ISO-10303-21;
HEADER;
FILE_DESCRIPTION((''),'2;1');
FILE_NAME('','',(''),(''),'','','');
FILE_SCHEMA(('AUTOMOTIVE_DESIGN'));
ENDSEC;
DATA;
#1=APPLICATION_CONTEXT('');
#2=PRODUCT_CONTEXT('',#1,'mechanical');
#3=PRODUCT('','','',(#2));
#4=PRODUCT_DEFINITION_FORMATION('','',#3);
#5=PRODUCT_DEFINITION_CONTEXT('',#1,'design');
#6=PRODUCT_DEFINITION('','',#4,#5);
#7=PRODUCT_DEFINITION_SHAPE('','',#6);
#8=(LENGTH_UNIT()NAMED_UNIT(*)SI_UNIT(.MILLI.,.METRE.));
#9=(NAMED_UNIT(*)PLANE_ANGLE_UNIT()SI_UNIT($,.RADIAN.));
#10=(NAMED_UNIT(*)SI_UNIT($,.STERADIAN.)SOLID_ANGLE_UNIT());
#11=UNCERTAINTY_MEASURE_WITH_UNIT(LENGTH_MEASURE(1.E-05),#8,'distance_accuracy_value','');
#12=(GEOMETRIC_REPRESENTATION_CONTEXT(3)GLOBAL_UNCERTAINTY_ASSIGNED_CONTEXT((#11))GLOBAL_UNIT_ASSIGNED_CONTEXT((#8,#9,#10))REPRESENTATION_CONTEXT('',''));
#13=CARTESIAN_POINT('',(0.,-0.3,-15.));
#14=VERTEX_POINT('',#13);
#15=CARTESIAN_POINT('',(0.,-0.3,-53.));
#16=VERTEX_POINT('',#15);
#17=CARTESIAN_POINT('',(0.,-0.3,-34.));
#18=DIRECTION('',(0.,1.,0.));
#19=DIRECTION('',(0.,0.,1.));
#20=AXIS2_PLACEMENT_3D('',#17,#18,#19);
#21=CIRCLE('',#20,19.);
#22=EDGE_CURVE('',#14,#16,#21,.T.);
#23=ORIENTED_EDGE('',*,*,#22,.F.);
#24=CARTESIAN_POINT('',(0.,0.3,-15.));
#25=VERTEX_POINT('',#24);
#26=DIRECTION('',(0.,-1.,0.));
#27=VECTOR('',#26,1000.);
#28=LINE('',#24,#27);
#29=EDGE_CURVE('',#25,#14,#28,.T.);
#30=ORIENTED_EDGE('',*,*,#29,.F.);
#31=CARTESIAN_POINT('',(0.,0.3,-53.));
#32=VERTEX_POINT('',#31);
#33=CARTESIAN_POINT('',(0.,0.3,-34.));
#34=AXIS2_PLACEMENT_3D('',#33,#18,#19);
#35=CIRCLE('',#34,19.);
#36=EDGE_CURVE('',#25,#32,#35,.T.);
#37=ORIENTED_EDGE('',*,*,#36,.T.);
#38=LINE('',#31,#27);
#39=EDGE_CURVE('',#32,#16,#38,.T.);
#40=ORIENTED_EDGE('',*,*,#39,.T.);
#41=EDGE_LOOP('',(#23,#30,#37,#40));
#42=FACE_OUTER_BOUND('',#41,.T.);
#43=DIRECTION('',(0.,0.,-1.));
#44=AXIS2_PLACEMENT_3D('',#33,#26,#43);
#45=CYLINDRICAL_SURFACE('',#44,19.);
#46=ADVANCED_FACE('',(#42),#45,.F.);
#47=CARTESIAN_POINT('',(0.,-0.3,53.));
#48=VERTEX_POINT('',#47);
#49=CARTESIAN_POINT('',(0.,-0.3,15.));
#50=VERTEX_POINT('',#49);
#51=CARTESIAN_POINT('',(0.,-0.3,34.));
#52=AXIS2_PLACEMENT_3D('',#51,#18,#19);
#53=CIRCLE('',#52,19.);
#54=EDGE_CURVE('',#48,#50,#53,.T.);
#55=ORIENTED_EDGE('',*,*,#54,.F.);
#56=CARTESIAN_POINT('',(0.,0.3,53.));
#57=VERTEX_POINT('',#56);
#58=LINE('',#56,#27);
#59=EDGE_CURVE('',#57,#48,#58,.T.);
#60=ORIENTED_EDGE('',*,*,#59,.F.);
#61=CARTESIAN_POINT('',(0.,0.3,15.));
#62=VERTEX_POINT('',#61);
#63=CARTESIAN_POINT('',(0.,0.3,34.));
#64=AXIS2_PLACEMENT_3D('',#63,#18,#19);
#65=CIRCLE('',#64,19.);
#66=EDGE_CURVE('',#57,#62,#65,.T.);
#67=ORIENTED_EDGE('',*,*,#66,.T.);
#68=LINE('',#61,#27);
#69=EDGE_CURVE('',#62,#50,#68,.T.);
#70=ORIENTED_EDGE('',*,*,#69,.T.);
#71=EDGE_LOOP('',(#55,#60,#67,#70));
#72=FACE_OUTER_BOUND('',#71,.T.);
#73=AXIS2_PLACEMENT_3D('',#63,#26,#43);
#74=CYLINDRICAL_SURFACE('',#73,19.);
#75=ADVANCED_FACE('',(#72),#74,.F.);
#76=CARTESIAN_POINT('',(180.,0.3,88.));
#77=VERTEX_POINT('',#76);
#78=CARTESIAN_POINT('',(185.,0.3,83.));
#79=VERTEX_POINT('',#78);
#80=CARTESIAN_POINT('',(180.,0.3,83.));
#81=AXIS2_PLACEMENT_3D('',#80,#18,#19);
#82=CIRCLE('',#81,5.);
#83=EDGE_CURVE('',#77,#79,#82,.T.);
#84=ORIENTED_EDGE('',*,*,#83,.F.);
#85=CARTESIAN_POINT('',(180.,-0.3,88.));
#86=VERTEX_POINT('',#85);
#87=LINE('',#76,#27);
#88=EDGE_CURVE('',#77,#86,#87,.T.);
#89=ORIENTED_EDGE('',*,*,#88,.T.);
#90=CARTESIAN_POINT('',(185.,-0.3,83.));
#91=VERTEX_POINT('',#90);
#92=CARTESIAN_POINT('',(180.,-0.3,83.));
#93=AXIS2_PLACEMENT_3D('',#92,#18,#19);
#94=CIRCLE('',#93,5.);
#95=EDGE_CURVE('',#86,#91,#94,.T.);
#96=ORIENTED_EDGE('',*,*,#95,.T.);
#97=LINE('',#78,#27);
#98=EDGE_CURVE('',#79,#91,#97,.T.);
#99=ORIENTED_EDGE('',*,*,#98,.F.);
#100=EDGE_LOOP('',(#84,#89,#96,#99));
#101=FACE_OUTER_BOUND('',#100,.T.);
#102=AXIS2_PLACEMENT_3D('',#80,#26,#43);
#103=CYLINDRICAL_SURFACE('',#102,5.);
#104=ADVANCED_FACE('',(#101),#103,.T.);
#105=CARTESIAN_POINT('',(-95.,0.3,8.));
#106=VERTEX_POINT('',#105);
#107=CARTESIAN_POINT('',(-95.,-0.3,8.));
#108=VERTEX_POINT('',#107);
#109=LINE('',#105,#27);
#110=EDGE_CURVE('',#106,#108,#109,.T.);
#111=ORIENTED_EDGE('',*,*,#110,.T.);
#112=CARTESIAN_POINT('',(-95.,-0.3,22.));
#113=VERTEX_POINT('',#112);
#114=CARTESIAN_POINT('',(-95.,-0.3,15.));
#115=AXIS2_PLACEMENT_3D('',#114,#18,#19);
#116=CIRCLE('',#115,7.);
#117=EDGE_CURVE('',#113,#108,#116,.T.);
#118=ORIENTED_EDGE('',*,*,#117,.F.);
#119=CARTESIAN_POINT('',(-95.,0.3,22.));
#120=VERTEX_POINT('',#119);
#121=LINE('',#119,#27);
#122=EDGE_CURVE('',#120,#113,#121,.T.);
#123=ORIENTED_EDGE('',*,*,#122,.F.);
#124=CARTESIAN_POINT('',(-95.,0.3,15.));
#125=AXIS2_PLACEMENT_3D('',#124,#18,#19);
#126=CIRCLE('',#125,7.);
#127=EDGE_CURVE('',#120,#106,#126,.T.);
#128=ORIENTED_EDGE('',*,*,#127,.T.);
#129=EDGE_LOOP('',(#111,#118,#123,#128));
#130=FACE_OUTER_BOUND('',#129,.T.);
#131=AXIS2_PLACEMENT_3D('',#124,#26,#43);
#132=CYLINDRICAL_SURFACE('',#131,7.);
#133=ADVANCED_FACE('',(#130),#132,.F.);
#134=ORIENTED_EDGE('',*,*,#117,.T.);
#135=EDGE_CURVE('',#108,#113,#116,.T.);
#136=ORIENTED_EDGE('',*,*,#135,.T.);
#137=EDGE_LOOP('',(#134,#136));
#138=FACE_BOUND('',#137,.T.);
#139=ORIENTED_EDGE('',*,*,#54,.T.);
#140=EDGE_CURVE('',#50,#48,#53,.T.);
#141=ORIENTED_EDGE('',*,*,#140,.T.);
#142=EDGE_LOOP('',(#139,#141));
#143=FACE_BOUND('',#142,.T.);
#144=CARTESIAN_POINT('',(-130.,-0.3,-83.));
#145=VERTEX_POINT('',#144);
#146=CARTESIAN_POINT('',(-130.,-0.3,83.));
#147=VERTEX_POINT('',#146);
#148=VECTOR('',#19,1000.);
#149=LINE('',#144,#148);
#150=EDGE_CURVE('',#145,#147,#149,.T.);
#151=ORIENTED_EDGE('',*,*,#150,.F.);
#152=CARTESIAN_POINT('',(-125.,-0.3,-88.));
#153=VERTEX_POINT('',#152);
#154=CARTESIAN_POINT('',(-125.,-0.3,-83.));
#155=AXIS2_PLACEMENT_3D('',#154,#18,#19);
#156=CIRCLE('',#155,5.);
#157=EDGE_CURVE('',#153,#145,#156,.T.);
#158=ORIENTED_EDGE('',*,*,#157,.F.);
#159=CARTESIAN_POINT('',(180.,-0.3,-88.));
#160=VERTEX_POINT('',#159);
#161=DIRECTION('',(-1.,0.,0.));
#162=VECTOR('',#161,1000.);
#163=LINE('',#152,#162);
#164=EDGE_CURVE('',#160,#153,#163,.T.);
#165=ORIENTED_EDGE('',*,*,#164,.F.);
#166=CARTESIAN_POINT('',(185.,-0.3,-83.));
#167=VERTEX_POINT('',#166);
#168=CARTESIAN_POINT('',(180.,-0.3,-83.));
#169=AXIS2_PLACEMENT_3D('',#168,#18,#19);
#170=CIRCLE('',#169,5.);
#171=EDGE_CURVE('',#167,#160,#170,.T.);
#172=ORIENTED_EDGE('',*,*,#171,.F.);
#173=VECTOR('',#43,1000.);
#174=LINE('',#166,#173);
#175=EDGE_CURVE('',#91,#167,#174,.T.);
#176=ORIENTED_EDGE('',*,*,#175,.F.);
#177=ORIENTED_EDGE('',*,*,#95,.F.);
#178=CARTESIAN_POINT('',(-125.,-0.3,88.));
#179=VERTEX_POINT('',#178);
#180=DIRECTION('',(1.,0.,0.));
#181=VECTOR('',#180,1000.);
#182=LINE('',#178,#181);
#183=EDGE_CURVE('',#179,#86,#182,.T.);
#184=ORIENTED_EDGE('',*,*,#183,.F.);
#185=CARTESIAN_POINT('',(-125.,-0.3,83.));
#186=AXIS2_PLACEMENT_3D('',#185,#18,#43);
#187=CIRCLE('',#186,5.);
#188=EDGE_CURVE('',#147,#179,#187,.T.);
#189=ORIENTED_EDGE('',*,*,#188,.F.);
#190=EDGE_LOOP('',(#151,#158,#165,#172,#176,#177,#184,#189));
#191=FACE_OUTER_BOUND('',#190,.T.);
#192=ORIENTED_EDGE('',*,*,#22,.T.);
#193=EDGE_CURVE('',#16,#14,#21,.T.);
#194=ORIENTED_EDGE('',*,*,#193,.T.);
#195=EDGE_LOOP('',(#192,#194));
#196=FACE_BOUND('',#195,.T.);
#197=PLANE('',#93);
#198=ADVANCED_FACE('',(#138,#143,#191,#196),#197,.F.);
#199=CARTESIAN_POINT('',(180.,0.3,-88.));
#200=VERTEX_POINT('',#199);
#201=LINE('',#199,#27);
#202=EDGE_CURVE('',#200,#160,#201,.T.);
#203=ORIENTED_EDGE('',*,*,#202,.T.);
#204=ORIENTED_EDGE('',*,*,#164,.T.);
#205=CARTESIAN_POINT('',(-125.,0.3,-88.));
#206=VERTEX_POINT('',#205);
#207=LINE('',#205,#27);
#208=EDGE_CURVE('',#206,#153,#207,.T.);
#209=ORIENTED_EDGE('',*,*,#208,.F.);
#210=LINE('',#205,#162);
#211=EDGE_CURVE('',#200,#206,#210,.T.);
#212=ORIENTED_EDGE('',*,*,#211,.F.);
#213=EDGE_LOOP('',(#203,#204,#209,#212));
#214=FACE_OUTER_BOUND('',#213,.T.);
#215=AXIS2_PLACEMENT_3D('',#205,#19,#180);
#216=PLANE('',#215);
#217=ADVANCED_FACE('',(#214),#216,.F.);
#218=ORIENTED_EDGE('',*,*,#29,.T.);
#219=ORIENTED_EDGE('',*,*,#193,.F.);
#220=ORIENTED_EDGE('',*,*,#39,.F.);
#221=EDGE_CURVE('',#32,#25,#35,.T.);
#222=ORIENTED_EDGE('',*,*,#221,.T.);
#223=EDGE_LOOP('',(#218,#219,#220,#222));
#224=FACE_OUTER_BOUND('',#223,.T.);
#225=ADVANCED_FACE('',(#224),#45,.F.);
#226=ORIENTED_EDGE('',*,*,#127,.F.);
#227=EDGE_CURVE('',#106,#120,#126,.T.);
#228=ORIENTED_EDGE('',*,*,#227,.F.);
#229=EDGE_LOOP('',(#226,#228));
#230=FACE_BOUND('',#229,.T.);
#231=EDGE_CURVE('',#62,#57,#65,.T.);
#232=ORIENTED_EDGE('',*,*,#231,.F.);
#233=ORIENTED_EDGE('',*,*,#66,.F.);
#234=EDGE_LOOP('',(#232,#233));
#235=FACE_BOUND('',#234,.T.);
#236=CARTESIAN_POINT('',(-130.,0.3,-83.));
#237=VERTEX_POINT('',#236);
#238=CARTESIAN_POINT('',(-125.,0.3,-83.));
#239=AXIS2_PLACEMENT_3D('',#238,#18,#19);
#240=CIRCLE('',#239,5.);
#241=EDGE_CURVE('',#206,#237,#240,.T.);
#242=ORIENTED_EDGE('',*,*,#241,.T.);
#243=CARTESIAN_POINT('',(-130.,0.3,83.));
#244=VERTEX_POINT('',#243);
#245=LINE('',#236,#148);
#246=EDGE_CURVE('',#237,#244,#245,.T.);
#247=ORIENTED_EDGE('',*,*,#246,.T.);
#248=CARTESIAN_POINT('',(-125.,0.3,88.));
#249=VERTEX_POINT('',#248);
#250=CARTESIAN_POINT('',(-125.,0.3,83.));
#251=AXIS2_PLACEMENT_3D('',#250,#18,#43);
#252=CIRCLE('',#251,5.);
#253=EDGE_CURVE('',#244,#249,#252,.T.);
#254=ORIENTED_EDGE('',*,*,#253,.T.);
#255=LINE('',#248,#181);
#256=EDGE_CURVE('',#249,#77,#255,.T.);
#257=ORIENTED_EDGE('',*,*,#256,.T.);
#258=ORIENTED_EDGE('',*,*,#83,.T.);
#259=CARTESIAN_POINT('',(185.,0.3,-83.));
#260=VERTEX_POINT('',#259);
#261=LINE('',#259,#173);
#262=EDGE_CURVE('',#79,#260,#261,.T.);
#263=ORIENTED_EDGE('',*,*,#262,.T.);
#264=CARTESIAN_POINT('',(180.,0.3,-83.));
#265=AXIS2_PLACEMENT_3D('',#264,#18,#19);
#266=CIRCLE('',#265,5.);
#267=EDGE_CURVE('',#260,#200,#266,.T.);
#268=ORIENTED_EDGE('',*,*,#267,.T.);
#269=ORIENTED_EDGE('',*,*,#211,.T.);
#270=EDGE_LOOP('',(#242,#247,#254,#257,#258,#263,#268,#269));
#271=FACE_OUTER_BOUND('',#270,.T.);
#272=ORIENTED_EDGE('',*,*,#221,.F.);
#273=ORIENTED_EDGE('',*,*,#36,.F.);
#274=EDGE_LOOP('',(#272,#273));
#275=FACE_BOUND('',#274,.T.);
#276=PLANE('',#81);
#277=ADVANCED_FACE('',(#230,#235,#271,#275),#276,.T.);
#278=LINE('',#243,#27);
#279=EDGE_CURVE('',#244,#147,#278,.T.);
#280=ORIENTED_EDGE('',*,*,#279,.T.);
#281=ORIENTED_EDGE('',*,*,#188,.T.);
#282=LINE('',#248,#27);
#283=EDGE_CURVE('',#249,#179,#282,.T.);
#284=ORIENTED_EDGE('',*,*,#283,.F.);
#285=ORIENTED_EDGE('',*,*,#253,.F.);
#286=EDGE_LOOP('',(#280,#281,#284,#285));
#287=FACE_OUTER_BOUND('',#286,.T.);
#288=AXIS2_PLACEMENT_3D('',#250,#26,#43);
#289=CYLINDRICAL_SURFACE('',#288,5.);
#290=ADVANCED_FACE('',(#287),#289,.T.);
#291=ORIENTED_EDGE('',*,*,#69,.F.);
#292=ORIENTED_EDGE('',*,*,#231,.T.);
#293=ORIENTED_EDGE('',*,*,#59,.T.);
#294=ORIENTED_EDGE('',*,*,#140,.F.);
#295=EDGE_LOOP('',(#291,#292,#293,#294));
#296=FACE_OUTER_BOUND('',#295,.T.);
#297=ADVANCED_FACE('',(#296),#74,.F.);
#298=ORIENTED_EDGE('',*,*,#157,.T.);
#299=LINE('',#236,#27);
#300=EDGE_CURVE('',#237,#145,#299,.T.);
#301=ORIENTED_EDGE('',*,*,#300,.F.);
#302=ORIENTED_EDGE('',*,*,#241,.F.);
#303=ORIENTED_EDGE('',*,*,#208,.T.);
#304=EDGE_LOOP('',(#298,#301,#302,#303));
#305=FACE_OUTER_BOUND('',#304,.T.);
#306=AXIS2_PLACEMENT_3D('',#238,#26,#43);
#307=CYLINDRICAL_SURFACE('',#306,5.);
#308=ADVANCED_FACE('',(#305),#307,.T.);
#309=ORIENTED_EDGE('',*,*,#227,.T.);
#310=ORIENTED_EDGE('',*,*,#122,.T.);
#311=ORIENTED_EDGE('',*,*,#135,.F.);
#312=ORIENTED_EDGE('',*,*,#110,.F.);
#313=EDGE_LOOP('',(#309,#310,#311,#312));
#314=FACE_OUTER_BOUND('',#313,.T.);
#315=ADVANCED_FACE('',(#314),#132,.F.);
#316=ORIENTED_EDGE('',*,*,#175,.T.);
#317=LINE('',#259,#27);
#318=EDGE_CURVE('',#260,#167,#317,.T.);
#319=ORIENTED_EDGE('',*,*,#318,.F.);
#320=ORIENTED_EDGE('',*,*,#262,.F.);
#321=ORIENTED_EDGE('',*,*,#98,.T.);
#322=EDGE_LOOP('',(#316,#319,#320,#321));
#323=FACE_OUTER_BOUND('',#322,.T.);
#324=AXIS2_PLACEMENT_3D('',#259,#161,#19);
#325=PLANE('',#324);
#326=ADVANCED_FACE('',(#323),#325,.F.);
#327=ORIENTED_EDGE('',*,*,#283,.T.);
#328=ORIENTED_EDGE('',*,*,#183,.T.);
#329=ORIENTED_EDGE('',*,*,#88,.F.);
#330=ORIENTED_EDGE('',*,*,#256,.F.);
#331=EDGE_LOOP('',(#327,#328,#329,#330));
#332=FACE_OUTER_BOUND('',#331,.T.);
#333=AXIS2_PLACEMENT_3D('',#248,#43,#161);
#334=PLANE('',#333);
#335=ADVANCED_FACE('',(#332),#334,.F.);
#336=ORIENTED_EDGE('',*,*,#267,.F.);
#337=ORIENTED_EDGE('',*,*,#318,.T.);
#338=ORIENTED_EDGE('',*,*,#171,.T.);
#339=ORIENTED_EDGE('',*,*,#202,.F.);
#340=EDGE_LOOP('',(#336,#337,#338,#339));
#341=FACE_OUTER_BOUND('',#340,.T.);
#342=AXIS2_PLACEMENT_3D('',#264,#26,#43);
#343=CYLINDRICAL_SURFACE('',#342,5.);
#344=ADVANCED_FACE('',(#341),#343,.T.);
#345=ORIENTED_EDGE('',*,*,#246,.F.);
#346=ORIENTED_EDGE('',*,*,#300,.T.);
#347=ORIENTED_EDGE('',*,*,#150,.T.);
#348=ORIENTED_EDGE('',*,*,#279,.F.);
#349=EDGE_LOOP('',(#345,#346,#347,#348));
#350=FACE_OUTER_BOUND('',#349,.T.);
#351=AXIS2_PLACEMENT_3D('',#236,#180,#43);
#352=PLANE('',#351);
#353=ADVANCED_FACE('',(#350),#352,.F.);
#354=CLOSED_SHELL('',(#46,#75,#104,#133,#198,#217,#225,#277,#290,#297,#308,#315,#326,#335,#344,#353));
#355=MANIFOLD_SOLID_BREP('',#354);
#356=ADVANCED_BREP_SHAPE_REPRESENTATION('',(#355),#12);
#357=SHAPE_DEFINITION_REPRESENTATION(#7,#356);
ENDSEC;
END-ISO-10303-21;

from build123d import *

# Parameters (mm, degrees)
SKETCH1_R           = 19
SKETCH1_R_2         = 7
BOSS_EXTRUDE1_DEPTH = 0.3


with BuildPart() as part:
    # Sketch1 → Boss-Extrude1 (new, symmetric)
    with BuildSketch(Plane(origin=(0, 0, 0), x_dir=(1, 0, 0), z_dir=(0, 1, 0))):
        with BuildLine():
            Line((-130, 83), (-130, -83))
            ThreePointArc((-130, -83), (-128.535533906, -86.535533906), (-125, -88))
            Line((-125, -88), (180, -88))
            ThreePointArc((180, -88), (183.535533906, -86.535533906), (185, -83))
            Line((185, -83), (185, 83))
            ThreePointArc((185, 83), (183.535533906, 86.535533906), (180, 88))
            Line((180, 88), (-125, 88))
            ThreePointArc((-125, 88), (-128.535533906, 86.535533906), (-130, 83))
        make_face()
        with Locations(Location((0, 34, 0), (0, 0, 270))):
            Circle(SKETCH1_R, mode=Mode.SUBTRACT)
        with Locations(Location((0, -34, 0), (0, 0, 270))):
            Circle(SKETCH1_R, mode=Mode.SUBTRACT)
        with Locations(Location((-95, -15, 0), (0, 0, 270))):
            Circle(SKETCH1_R_2, mode=Mode.SUBTRACT)
    extrude(amount=BOSS_EXTRUDE1_DEPTH, both=True)


solid = part.part
